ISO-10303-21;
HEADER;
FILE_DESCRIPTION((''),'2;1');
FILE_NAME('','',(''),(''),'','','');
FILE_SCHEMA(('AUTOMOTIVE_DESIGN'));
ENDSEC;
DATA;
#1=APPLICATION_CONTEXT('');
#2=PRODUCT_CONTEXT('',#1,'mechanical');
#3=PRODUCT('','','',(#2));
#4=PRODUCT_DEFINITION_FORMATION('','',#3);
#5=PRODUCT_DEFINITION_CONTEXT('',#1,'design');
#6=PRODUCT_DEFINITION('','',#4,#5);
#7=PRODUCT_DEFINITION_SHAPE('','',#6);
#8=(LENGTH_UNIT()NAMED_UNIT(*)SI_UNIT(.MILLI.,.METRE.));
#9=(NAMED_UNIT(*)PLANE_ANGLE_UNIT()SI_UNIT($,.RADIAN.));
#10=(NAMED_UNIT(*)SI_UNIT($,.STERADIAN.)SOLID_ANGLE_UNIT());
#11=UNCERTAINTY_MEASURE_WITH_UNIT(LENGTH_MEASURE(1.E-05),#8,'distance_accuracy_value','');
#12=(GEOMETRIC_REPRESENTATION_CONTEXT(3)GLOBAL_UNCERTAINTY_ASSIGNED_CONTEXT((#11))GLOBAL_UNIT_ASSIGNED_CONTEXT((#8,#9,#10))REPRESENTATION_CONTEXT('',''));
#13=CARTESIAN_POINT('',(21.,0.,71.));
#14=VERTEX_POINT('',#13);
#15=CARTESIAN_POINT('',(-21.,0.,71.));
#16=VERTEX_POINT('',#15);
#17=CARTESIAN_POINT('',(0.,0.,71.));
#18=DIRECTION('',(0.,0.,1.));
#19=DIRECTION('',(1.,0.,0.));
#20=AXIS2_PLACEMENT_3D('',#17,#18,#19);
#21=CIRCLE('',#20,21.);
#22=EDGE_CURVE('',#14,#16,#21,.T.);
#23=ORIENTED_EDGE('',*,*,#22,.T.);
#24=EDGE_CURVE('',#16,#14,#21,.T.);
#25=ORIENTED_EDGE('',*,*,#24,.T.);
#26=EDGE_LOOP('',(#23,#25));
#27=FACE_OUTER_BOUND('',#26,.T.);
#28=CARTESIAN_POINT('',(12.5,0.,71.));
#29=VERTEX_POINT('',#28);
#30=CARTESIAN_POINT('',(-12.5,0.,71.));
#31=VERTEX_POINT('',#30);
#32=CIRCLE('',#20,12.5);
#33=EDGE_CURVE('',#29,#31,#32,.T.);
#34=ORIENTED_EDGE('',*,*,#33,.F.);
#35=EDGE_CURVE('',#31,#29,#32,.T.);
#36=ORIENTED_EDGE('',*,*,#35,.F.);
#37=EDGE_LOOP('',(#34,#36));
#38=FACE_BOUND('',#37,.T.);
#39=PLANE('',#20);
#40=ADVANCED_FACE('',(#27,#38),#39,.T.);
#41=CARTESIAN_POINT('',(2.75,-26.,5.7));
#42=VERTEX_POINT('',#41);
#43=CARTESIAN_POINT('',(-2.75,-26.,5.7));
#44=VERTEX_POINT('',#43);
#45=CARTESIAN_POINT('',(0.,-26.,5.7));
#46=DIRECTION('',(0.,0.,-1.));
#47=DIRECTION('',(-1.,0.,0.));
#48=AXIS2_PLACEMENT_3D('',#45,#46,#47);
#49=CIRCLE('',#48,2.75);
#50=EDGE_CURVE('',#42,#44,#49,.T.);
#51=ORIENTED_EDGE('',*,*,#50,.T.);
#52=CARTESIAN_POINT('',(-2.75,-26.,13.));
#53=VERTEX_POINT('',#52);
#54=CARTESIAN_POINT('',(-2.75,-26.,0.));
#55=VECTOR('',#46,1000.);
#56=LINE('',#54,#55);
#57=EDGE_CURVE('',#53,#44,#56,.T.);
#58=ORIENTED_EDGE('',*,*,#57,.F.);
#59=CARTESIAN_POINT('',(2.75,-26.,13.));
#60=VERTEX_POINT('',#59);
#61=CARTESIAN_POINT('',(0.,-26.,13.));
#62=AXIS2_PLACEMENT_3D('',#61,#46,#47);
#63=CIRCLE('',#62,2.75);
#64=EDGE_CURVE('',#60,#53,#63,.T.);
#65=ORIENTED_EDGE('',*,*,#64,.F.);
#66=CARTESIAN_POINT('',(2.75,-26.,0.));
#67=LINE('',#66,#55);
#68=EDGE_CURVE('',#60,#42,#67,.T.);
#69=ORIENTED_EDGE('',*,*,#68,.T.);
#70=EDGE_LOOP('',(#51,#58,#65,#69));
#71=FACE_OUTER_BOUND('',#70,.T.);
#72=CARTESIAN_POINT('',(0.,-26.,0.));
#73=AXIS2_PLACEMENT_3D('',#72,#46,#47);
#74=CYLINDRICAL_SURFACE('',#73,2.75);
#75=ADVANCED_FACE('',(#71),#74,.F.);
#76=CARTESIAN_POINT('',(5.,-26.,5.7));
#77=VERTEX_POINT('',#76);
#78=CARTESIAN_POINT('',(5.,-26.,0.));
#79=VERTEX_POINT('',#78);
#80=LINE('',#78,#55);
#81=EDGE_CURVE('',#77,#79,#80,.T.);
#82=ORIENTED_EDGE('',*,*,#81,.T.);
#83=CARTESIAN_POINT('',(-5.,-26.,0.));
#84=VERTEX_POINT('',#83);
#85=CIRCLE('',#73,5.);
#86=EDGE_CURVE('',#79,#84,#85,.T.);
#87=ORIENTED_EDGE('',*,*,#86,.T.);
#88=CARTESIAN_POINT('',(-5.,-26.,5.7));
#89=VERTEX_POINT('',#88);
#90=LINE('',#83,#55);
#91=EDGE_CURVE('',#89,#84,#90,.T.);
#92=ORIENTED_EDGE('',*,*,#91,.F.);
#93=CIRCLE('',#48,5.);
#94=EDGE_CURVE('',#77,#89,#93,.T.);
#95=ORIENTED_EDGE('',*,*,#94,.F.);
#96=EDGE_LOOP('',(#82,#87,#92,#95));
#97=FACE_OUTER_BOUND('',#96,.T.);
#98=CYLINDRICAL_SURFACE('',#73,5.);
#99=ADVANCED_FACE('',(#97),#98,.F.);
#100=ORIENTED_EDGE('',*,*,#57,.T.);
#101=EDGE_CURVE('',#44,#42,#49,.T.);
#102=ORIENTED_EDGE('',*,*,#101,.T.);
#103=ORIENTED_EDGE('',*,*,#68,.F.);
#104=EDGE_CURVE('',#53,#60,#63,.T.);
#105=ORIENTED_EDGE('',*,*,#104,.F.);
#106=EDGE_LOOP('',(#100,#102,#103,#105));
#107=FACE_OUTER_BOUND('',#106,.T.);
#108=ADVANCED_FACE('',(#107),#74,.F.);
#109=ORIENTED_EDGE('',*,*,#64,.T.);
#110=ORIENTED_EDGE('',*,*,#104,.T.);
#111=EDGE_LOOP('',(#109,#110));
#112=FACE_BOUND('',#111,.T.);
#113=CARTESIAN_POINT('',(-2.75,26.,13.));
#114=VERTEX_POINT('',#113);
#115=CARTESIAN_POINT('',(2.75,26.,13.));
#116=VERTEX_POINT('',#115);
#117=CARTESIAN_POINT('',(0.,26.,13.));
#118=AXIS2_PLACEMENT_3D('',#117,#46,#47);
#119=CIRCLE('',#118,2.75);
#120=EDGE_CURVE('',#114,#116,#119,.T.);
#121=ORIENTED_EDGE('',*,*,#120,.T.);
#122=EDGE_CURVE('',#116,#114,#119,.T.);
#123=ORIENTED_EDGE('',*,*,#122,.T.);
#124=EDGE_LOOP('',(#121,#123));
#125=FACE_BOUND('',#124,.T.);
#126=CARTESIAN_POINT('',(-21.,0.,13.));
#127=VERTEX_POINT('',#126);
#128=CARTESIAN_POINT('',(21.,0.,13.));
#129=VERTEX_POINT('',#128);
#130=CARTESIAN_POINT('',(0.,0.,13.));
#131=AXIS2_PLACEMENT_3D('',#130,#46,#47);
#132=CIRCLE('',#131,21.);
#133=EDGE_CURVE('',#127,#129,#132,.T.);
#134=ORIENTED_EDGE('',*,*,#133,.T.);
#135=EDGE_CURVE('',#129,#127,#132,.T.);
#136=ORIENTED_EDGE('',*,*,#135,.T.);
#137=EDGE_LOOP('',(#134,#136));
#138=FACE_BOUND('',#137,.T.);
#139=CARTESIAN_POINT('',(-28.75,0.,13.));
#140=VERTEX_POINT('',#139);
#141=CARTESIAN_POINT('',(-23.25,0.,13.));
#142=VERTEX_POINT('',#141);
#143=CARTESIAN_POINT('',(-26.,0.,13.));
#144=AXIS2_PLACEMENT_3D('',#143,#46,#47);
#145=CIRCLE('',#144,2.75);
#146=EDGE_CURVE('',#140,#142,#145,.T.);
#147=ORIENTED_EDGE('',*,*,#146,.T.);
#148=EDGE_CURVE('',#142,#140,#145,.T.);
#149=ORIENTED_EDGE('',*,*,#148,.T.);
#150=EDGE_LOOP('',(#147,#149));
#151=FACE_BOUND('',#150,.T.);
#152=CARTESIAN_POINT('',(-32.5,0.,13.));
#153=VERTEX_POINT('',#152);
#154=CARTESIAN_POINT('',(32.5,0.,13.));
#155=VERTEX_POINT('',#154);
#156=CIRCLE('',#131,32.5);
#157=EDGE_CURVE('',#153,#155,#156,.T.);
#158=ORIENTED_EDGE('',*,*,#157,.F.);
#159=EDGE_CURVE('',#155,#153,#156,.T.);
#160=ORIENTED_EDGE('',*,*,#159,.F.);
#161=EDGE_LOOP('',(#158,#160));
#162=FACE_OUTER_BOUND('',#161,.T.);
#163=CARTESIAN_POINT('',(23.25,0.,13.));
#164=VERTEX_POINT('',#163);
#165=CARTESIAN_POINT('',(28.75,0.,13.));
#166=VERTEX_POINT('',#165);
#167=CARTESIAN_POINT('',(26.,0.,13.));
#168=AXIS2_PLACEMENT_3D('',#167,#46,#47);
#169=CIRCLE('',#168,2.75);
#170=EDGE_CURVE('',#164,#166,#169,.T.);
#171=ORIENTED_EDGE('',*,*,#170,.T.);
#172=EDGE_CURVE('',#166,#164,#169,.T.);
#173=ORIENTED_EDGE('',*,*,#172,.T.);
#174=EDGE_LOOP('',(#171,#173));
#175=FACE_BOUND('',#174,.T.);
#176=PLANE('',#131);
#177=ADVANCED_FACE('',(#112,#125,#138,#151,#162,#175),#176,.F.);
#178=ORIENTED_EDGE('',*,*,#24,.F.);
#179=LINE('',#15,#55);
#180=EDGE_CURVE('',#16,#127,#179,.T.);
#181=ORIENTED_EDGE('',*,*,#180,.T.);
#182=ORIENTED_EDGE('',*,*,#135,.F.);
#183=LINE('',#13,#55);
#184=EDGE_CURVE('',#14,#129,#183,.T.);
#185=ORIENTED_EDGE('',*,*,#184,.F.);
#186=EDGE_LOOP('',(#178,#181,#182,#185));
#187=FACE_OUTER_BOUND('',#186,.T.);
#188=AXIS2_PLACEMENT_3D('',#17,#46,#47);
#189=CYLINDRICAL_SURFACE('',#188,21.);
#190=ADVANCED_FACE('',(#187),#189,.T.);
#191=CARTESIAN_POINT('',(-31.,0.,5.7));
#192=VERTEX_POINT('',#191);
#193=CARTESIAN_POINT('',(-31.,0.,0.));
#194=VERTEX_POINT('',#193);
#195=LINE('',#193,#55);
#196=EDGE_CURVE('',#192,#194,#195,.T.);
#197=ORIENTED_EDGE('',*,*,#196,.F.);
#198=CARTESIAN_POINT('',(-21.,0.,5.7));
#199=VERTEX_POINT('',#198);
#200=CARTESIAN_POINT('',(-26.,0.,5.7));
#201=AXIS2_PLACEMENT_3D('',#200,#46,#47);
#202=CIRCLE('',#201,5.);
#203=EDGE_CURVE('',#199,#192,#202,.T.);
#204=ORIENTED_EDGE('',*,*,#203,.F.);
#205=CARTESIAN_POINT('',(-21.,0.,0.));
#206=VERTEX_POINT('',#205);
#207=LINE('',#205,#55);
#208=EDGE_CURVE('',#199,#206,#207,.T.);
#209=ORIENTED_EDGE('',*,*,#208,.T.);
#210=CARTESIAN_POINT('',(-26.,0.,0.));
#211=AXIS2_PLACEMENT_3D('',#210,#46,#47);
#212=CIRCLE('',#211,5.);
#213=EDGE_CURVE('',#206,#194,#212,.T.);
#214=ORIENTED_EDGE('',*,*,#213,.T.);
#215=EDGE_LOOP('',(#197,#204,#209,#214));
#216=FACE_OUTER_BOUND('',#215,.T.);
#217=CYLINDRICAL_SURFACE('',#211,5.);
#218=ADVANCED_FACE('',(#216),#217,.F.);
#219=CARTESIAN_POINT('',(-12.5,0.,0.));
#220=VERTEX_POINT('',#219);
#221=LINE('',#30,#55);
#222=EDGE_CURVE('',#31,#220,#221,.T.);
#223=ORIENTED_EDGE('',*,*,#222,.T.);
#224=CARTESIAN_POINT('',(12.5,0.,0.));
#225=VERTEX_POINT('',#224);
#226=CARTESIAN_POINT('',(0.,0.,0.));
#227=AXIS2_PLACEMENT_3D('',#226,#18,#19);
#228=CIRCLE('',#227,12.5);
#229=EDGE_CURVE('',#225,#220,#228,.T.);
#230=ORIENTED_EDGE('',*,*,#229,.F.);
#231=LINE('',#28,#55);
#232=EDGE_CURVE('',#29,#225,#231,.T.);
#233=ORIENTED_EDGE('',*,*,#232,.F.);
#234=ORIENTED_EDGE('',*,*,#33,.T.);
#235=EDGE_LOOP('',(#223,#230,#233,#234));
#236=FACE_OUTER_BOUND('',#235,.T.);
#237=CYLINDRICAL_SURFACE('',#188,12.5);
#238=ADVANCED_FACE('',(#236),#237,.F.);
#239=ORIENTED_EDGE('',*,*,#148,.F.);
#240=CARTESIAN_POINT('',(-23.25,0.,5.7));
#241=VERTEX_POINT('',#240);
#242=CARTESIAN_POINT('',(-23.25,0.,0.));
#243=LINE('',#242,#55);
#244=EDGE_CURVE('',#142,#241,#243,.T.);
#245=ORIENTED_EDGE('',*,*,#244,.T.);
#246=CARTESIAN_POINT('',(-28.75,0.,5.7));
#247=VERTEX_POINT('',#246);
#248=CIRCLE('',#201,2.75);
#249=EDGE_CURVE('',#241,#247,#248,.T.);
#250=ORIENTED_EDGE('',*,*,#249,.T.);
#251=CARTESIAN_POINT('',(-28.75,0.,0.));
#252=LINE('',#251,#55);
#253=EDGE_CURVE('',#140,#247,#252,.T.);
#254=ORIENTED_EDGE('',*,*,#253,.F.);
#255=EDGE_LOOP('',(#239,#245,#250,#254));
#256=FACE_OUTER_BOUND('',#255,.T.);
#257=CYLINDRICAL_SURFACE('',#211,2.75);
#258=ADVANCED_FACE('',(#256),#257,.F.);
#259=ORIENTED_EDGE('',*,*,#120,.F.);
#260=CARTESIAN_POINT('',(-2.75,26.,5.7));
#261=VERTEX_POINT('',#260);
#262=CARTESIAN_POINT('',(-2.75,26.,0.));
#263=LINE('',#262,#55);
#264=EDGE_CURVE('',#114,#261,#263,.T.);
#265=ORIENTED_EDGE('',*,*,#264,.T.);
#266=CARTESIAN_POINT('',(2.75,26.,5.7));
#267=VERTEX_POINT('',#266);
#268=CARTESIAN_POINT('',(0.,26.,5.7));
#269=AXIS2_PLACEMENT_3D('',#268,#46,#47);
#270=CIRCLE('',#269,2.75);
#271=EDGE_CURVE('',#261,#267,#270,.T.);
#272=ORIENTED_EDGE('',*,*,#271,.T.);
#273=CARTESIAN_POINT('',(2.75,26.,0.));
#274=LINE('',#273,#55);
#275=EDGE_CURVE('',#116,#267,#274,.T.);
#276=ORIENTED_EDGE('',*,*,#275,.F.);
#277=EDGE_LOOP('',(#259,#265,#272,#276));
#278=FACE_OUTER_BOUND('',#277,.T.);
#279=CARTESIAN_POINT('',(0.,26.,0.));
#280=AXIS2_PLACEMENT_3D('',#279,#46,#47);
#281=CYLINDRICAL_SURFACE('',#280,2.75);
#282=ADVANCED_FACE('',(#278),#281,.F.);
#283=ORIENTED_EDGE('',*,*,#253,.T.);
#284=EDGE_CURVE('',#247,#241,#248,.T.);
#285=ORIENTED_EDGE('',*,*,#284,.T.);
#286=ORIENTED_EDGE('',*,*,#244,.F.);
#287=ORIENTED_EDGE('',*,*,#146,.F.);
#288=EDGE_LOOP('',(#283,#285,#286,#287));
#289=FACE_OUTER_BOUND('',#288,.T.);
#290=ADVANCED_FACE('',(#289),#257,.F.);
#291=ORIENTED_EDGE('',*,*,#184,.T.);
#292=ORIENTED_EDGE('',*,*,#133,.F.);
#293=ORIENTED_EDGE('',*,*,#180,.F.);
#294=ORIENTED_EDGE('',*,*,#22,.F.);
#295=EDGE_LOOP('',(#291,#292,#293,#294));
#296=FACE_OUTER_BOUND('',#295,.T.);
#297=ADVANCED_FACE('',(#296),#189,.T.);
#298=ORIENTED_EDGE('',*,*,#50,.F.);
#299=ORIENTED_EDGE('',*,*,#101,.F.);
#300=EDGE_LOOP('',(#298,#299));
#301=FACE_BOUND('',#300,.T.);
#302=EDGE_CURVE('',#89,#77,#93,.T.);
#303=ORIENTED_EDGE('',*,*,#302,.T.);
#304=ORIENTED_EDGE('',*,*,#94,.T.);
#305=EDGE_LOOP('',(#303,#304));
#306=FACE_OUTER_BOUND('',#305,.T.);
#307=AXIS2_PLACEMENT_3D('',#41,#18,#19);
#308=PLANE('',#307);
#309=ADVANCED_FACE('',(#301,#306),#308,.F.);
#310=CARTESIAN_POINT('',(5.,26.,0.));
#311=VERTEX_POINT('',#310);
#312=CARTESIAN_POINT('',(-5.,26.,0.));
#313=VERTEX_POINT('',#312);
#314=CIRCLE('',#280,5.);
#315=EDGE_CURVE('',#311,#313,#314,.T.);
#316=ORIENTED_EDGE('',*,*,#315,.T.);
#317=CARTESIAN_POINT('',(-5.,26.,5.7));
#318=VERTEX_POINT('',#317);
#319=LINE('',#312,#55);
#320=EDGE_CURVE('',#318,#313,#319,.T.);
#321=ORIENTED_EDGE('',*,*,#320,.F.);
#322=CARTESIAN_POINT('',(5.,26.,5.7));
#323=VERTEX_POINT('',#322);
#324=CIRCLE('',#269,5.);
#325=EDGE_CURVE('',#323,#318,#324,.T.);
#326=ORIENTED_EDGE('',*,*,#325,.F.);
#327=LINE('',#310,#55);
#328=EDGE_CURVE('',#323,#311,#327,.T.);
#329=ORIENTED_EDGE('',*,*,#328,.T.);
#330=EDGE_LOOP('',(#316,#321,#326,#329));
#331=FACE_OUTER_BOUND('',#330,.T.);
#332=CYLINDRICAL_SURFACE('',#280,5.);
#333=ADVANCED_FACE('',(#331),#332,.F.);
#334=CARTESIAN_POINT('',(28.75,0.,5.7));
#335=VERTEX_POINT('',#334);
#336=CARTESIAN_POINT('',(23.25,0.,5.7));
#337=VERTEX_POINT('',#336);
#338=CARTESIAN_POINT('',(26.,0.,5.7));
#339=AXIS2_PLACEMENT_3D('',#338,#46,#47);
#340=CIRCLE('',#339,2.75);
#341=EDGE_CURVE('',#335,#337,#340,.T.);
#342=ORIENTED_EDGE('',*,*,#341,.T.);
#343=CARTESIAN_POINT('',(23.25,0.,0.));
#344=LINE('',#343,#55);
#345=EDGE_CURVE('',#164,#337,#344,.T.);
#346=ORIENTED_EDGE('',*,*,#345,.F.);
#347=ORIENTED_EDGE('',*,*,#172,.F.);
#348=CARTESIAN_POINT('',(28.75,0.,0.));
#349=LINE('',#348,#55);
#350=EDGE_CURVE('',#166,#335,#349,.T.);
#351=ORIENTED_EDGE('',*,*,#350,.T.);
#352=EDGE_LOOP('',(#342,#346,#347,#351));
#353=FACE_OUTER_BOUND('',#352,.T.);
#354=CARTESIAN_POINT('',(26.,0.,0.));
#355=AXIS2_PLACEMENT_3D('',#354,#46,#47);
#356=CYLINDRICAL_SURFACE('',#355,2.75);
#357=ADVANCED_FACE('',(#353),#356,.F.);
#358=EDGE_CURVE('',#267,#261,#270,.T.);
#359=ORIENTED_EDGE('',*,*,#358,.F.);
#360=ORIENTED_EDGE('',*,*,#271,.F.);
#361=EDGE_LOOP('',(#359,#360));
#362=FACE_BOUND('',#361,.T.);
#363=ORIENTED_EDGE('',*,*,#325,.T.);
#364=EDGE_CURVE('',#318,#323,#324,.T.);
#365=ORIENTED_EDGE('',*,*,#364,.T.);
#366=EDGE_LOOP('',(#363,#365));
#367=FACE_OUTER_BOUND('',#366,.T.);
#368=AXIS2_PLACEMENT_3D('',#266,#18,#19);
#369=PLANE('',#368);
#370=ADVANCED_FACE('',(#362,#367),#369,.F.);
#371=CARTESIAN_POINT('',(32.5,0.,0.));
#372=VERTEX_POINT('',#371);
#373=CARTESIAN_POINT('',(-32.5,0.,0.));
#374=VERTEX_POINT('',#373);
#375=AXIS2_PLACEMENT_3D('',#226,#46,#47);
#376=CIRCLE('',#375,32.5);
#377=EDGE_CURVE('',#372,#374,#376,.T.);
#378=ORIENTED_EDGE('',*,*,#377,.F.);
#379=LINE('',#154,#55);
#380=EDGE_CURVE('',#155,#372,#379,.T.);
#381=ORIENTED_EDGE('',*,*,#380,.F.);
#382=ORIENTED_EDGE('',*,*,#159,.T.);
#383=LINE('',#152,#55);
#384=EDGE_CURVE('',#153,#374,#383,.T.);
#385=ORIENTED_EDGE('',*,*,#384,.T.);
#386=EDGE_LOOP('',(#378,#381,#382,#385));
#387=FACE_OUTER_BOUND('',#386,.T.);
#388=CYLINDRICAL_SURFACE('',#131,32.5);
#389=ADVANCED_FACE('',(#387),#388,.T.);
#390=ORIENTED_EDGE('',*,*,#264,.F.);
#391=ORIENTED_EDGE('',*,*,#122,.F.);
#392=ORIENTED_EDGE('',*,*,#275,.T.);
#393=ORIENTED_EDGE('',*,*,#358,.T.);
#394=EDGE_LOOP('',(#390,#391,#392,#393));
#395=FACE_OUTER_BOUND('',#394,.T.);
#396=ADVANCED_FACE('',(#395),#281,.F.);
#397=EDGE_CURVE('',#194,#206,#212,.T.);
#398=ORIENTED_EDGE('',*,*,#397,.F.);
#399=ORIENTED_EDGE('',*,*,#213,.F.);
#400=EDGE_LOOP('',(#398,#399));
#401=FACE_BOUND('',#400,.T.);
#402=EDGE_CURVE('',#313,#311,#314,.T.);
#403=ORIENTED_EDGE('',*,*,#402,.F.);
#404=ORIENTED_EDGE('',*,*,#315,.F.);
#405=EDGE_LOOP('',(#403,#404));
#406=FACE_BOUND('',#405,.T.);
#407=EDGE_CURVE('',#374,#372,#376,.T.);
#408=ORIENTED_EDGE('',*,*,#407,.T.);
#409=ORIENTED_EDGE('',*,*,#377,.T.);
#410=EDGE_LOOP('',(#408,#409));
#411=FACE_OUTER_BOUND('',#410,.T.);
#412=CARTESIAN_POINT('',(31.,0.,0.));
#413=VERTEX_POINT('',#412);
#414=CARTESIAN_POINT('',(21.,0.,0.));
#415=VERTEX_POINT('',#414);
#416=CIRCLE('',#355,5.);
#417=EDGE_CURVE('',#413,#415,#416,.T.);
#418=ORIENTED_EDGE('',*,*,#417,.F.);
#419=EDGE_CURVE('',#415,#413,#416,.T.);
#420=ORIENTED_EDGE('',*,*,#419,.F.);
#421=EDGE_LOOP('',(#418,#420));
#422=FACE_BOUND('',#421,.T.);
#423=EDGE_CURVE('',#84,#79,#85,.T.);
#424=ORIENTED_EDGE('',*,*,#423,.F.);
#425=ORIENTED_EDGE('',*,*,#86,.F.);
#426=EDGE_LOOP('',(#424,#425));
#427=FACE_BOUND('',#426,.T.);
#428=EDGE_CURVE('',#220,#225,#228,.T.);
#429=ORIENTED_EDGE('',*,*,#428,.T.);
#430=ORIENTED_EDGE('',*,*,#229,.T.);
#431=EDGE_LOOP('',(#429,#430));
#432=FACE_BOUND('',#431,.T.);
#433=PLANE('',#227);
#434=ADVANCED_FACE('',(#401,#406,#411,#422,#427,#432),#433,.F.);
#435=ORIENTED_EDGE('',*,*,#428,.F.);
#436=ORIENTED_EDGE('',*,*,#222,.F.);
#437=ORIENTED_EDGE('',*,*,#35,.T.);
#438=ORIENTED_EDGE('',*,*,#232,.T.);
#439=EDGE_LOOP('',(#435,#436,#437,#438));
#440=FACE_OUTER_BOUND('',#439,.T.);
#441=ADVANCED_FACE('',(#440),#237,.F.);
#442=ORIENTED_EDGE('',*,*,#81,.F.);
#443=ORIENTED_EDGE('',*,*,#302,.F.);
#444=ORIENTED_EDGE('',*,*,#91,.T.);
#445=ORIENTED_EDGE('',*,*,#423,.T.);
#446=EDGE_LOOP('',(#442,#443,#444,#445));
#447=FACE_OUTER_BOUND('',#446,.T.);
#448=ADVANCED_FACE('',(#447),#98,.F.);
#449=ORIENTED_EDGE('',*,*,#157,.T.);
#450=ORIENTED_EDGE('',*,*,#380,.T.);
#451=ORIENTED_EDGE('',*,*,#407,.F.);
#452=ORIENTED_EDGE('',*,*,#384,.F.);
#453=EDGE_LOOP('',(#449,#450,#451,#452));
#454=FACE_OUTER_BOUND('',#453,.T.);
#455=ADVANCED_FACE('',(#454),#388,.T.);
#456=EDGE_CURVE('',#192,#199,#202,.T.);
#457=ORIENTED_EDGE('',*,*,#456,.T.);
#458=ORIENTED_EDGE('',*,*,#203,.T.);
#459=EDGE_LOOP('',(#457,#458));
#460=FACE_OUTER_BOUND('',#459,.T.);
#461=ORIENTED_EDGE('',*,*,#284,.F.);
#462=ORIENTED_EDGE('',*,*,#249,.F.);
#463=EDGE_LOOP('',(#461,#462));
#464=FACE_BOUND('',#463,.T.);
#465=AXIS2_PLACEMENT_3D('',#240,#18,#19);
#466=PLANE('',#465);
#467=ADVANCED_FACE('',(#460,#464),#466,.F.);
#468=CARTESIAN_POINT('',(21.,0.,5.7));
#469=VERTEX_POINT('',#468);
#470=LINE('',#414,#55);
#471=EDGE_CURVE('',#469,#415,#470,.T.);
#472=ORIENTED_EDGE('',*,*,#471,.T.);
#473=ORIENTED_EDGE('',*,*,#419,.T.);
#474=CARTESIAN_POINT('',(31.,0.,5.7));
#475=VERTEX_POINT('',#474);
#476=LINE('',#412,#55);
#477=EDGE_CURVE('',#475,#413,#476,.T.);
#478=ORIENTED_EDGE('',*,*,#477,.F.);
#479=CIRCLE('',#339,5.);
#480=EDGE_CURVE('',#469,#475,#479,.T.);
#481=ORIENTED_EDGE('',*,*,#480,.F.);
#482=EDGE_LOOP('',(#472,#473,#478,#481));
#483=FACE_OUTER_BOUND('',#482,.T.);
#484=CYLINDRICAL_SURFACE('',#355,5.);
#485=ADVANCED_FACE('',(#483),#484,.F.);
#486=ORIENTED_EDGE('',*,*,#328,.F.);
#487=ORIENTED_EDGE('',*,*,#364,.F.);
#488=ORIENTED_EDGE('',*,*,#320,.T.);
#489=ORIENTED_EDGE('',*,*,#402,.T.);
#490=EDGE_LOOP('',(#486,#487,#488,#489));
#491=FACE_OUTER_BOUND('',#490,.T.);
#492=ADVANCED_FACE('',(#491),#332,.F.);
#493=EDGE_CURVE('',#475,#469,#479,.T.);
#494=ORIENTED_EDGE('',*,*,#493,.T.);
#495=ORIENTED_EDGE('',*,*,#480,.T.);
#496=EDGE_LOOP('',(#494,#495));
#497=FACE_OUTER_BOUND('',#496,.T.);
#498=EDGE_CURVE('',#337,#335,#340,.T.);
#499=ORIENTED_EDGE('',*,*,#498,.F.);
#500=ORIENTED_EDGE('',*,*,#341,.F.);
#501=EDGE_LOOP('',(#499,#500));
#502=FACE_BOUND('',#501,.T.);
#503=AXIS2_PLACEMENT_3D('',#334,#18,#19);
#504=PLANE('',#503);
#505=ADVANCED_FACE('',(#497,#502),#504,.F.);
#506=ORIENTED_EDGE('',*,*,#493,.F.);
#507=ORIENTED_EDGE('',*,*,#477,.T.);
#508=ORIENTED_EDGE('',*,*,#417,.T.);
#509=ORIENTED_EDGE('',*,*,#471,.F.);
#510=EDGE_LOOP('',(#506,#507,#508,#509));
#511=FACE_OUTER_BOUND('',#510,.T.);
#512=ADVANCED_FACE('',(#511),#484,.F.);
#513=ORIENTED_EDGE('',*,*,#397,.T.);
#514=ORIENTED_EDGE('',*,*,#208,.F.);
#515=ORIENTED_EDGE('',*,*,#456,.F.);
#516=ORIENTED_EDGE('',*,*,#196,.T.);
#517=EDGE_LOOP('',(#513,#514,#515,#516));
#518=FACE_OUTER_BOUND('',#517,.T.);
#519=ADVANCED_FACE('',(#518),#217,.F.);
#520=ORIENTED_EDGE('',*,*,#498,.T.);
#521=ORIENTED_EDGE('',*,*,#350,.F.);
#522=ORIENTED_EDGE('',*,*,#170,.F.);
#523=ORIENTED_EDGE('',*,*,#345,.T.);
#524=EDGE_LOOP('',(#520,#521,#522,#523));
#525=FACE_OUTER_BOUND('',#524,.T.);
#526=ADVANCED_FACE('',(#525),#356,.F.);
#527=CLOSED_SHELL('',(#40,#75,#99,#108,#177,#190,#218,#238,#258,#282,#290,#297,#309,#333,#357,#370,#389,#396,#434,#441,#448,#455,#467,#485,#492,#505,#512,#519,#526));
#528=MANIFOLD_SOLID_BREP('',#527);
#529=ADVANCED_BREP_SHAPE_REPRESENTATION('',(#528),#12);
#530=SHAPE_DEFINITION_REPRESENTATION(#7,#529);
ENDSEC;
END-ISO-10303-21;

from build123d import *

# Parameters (mm, degrees)
SKETCH_1_R                = 21
SKETCH_1_R_2              = 12.5
EXTRUDE_1_DEPTH           = 71
SKETCH_2_R                = 32.5
SKETCH_2_R_2              = 12.5
EXTRUDE_2_DEPTH           = 13
HOLE_WIZARD_1_D           = 5.5
HOLE_WIZARD_1_CBORE_D     = 10
HOLE_WIZARD_1_CBORE_DEPTH = 5.7


with BuildPart() as part:
    # 草图1 → 凸台-拉伸1 (new body)
    with BuildSketch(Plane.XY):
        Circle(SKETCH_1_R)
        Circle(SKETCH_1_R_2, mode=Mode.SUBTRACT)
    extrude(amount=EXTRUDE_1_DEPTH)

    # 草图2 → 凸台-拉伸2 (add)
    with BuildSketch(Plane(origin=(0, 0, 0), x_dir=(-1, 0, 0), z_dir=(0, 0, -1))):
        Circle(SKETCH_2_R)
        with Locations(Location((0, 0, 0), (0, 0, 180))):
            Circle(SKETCH_2_R_2, mode=Mode.SUBTRACT)
    extrude(amount=-EXTRUDE_2_DEPTH)

    # 打孔尺寸(%根据)内六角圆柱头螺钉的类型1 (through all)
    with Locations(Plane(origin=(0, 26, 0), x_dir=(-1, 0, 0), z_dir=(0, 0, -1))):
        with Locations((0, 0), (26, -26), (0, -52), (-26, -26)):
            CounterBoreHole(HOLE_WIZARD_1_D / 2, HOLE_WIZARD_1_CBORE_D / 2, HOLE_WIZARD_1_CBORE_DEPTH)


solid = part.part
